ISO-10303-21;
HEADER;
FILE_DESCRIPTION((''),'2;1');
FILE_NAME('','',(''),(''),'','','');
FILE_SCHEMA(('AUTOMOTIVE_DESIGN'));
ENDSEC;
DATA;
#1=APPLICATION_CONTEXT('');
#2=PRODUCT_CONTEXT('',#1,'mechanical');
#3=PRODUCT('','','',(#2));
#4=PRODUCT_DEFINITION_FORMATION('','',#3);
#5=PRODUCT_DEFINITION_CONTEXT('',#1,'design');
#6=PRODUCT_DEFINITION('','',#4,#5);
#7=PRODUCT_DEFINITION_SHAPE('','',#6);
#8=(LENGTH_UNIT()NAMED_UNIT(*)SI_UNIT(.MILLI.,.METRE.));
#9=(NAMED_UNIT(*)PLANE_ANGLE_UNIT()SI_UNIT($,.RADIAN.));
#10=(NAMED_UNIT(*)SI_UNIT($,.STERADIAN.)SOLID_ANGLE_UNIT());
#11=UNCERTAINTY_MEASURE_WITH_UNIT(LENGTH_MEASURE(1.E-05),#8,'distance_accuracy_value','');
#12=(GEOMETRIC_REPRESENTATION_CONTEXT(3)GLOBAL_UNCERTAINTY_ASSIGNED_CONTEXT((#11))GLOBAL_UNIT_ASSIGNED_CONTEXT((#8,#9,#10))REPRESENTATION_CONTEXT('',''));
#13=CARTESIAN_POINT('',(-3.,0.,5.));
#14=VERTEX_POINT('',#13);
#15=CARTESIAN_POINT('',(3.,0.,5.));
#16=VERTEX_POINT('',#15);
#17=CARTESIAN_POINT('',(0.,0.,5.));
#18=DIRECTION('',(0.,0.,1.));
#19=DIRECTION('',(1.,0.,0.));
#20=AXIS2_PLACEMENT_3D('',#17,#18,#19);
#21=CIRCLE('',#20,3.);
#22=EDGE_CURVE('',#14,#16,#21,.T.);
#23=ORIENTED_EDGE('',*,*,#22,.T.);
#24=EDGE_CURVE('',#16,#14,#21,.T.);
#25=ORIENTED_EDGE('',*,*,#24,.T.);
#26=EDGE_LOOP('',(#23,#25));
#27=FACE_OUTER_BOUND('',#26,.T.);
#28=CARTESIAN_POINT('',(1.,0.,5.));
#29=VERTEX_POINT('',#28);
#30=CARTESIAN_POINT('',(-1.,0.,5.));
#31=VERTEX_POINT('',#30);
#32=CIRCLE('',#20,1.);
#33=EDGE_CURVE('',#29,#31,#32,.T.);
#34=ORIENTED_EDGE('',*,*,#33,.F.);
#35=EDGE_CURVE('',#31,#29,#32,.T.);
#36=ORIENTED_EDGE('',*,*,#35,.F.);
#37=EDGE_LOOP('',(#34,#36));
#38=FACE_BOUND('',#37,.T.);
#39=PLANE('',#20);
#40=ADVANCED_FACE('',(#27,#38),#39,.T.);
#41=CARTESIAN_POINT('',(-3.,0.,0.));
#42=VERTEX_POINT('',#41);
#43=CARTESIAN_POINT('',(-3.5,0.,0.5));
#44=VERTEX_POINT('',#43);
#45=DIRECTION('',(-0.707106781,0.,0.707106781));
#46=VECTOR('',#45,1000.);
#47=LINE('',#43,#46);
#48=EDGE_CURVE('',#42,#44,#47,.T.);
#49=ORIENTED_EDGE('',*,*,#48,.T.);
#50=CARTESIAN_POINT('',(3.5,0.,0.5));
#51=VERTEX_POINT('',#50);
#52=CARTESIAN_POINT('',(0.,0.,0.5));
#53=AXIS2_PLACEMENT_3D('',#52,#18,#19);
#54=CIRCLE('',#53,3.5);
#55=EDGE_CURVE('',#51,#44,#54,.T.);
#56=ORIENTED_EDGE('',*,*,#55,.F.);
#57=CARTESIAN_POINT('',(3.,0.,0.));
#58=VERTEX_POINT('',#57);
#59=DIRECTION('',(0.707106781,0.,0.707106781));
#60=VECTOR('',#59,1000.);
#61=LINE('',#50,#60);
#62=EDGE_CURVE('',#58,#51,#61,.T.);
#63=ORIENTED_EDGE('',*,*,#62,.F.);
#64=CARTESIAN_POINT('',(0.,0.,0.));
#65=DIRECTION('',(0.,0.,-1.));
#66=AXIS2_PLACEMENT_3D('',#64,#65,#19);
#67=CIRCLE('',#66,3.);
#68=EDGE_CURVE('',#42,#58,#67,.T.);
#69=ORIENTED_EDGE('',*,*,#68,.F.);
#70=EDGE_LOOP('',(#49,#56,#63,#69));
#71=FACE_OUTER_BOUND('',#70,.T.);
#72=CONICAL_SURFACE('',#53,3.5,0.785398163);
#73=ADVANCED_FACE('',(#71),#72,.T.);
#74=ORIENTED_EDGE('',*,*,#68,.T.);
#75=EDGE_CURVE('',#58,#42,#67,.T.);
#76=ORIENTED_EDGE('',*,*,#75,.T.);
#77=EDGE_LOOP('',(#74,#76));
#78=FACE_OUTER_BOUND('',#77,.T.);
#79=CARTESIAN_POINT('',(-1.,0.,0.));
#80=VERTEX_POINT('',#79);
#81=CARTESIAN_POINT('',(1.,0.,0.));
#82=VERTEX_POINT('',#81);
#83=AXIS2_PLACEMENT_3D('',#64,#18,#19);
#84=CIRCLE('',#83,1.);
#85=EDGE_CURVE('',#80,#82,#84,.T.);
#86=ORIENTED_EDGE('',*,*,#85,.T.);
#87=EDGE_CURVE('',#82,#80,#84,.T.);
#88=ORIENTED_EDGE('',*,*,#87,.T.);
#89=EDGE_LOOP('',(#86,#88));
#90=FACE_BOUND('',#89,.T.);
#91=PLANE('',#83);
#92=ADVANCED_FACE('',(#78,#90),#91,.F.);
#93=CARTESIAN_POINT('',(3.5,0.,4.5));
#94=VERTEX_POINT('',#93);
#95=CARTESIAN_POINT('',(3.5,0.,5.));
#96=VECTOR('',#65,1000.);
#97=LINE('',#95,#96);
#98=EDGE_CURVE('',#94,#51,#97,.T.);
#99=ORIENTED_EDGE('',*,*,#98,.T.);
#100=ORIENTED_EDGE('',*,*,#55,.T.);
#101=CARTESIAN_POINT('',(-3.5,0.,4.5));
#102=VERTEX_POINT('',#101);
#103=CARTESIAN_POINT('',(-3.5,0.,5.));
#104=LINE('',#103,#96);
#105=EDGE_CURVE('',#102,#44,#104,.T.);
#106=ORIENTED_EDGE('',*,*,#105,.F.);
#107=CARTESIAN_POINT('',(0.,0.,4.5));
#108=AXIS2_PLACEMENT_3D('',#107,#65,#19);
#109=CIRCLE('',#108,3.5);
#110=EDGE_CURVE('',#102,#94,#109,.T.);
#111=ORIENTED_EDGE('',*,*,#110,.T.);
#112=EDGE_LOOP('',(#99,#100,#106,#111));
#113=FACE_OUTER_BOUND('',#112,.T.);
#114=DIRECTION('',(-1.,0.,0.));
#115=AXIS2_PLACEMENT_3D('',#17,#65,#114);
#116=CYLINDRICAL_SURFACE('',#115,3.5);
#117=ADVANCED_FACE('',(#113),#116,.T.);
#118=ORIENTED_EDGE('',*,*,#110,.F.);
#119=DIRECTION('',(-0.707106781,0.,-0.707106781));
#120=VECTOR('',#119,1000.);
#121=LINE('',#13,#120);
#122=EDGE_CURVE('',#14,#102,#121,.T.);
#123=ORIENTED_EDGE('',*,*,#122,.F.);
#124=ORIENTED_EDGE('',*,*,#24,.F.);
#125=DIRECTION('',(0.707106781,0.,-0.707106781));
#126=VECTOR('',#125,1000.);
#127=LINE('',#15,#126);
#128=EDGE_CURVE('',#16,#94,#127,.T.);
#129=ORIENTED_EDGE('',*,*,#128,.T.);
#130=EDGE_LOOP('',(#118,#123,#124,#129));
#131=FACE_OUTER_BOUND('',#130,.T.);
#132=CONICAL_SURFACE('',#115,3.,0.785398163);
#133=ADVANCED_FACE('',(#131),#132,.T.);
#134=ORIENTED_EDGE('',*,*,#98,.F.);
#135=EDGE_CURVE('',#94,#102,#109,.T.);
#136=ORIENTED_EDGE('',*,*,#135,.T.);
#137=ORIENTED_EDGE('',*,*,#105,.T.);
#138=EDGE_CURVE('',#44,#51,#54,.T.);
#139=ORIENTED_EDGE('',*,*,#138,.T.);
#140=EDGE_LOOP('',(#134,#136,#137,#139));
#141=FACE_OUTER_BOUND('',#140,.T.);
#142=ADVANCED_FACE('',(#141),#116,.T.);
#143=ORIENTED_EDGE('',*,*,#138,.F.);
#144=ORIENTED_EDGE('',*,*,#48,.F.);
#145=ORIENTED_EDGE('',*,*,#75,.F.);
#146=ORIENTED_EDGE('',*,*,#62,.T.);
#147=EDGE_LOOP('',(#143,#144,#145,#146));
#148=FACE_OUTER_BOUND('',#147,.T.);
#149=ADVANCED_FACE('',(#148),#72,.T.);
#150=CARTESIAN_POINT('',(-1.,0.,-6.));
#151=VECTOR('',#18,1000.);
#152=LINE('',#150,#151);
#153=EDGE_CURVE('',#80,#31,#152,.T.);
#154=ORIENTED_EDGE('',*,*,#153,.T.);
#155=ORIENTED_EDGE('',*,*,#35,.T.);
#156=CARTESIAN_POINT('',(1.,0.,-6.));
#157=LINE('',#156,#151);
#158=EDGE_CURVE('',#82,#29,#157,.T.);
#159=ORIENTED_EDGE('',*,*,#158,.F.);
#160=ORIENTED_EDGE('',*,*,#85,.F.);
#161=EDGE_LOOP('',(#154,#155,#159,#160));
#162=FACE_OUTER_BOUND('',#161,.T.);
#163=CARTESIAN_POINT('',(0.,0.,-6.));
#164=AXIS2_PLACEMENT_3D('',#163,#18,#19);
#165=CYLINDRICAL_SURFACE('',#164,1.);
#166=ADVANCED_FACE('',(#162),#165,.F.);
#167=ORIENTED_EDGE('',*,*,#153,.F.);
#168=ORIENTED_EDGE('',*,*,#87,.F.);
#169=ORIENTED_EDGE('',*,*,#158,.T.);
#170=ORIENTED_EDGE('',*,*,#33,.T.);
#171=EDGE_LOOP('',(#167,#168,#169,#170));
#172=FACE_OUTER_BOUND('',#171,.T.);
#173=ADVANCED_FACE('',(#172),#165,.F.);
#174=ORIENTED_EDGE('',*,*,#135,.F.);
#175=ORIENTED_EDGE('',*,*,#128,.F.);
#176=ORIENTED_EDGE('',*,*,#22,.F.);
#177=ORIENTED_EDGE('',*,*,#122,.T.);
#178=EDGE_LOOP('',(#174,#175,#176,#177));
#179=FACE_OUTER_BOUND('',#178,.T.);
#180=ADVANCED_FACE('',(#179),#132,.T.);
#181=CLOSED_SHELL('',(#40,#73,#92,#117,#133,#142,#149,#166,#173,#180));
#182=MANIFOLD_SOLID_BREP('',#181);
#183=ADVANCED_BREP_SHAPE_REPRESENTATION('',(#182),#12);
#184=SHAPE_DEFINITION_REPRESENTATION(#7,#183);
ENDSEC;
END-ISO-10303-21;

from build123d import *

# Parameters (mm, degrees)
SKETCH1_R           = 3.5
BOSS_EXTRUDE1_DEPTH = 5
SKETCH2_R           = 1
CUT_EXTRUDE1_DEPTH  = 11
CHAMFER1_SIZE       = 0.5


with BuildPart() as part:
    # Sketch1 → Boss-Extrude1 (new body)
    with BuildSketch(Plane.XY):
        Circle(SKETCH1_R)
    extrude(amount=BOSS_EXTRUDE1_DEPTH)

    # Sketch2 → Cut-Extrude1 (cut)
    with BuildSketch(Plane.XY.offset(5)):
        Circle(SKETCH2_R)
    extrude(amount=-CUT_EXTRUDE1_DEPTH, mode=Mode.SUBTRACT)

    # Chamfer1
    chamfer1_edges = [part.edges().sort_by_distance(p)[0] for p in [
        (-3.5, 0, 0),
        (-3.5, 0, 5),
    ]]
    chamfer(chamfer1_edges, length=CHAMFER1_SIZE)


solid = part.part
